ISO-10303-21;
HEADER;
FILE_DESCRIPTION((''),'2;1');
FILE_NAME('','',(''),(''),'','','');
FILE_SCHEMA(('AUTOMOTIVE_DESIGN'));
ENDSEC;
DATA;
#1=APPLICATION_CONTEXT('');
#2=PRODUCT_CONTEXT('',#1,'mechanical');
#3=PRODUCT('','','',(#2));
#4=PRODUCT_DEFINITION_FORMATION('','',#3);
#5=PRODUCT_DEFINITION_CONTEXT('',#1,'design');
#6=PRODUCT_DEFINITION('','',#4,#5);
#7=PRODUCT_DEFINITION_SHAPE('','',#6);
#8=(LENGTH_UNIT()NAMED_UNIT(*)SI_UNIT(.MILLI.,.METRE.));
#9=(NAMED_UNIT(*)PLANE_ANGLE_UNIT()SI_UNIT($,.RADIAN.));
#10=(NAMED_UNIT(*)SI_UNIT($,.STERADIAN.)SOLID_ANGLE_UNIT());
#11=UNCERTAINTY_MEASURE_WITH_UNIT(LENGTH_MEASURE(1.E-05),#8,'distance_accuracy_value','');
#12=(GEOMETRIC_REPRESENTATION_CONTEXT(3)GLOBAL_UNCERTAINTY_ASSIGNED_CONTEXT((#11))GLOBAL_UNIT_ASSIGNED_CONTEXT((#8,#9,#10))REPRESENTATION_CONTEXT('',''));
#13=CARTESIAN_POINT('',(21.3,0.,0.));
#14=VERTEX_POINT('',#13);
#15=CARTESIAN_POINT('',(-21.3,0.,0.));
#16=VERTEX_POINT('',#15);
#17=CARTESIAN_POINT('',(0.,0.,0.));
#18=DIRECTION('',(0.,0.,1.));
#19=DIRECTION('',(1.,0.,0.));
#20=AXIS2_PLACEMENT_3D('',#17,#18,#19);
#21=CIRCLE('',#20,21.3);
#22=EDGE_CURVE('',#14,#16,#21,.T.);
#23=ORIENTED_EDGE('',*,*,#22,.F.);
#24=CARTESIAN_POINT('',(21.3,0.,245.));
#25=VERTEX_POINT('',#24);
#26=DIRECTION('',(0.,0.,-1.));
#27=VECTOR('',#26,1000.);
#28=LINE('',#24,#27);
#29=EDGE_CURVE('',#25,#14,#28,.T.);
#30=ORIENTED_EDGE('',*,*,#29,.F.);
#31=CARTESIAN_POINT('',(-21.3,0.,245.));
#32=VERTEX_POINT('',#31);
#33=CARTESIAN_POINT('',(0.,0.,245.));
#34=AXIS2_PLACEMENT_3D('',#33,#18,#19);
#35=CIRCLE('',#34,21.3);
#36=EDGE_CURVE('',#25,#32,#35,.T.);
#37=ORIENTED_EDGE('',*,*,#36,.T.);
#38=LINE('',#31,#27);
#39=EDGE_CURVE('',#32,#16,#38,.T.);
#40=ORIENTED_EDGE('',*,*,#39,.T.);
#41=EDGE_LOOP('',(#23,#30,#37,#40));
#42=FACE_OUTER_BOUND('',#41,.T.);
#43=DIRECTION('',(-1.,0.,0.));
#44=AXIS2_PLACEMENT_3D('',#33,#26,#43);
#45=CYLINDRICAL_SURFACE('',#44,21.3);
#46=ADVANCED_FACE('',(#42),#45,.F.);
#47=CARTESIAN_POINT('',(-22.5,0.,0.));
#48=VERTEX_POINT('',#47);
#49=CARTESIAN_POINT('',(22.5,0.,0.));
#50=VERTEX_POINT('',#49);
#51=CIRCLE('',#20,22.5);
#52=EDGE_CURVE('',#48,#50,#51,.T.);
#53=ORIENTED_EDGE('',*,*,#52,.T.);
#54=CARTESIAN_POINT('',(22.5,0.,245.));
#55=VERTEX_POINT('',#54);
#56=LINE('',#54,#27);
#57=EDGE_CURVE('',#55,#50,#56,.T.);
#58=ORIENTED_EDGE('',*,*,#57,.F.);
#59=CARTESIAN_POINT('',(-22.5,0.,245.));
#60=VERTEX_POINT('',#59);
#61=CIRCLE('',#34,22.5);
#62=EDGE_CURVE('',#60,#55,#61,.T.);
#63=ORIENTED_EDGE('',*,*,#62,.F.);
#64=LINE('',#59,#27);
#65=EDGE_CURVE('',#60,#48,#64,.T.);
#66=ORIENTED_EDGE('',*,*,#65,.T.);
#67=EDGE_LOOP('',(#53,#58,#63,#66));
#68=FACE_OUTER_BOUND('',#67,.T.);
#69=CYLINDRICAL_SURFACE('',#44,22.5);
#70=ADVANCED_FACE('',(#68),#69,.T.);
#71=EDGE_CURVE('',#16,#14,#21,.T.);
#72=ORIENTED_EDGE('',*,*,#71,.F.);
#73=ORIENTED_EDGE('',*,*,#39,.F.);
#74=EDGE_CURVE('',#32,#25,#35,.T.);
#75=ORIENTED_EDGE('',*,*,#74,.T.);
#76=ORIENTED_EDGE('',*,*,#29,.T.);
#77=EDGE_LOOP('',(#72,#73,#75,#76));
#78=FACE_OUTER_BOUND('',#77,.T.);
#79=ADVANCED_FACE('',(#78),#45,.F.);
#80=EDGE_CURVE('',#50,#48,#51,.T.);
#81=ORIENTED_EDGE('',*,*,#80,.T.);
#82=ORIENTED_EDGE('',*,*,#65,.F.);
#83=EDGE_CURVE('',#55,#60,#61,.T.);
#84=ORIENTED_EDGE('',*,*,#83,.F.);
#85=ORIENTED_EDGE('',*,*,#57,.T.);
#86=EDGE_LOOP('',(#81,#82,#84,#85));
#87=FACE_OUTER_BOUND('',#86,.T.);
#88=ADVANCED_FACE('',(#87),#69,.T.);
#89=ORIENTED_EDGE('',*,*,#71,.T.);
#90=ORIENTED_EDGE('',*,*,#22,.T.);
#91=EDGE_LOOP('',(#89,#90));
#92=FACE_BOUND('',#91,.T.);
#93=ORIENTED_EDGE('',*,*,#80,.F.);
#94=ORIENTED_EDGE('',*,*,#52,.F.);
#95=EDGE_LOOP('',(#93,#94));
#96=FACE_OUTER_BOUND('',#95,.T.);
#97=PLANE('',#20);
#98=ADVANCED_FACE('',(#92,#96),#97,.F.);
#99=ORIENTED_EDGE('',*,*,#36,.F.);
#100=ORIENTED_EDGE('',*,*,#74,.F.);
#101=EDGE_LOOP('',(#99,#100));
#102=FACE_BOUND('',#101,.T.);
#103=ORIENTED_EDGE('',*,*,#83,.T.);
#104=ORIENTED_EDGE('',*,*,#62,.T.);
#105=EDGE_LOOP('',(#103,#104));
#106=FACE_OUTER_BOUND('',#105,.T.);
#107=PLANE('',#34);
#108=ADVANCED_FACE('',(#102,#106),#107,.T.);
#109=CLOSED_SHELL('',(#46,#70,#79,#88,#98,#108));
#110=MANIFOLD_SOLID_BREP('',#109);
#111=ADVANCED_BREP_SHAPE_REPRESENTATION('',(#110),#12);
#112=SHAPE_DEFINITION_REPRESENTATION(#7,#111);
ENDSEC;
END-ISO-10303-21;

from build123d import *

# Parameters (mm, degrees)
SKETCH1_R           = 22.5
SKETCH1_R_2         = 21.3
BOSS_EXTRUDE1_DEPTH = 245


with BuildPart() as part:
    # Sketch1 → Boss-Extrude1 (new body)
    with BuildSketch(Plane.XY):
        Circle(SKETCH1_R)
        Circle(SKETCH1_R_2, mode=Mode.SUBTRACT)
    extrude(amount=BOSS_EXTRUDE1_DEPTH)


solid = part.part
